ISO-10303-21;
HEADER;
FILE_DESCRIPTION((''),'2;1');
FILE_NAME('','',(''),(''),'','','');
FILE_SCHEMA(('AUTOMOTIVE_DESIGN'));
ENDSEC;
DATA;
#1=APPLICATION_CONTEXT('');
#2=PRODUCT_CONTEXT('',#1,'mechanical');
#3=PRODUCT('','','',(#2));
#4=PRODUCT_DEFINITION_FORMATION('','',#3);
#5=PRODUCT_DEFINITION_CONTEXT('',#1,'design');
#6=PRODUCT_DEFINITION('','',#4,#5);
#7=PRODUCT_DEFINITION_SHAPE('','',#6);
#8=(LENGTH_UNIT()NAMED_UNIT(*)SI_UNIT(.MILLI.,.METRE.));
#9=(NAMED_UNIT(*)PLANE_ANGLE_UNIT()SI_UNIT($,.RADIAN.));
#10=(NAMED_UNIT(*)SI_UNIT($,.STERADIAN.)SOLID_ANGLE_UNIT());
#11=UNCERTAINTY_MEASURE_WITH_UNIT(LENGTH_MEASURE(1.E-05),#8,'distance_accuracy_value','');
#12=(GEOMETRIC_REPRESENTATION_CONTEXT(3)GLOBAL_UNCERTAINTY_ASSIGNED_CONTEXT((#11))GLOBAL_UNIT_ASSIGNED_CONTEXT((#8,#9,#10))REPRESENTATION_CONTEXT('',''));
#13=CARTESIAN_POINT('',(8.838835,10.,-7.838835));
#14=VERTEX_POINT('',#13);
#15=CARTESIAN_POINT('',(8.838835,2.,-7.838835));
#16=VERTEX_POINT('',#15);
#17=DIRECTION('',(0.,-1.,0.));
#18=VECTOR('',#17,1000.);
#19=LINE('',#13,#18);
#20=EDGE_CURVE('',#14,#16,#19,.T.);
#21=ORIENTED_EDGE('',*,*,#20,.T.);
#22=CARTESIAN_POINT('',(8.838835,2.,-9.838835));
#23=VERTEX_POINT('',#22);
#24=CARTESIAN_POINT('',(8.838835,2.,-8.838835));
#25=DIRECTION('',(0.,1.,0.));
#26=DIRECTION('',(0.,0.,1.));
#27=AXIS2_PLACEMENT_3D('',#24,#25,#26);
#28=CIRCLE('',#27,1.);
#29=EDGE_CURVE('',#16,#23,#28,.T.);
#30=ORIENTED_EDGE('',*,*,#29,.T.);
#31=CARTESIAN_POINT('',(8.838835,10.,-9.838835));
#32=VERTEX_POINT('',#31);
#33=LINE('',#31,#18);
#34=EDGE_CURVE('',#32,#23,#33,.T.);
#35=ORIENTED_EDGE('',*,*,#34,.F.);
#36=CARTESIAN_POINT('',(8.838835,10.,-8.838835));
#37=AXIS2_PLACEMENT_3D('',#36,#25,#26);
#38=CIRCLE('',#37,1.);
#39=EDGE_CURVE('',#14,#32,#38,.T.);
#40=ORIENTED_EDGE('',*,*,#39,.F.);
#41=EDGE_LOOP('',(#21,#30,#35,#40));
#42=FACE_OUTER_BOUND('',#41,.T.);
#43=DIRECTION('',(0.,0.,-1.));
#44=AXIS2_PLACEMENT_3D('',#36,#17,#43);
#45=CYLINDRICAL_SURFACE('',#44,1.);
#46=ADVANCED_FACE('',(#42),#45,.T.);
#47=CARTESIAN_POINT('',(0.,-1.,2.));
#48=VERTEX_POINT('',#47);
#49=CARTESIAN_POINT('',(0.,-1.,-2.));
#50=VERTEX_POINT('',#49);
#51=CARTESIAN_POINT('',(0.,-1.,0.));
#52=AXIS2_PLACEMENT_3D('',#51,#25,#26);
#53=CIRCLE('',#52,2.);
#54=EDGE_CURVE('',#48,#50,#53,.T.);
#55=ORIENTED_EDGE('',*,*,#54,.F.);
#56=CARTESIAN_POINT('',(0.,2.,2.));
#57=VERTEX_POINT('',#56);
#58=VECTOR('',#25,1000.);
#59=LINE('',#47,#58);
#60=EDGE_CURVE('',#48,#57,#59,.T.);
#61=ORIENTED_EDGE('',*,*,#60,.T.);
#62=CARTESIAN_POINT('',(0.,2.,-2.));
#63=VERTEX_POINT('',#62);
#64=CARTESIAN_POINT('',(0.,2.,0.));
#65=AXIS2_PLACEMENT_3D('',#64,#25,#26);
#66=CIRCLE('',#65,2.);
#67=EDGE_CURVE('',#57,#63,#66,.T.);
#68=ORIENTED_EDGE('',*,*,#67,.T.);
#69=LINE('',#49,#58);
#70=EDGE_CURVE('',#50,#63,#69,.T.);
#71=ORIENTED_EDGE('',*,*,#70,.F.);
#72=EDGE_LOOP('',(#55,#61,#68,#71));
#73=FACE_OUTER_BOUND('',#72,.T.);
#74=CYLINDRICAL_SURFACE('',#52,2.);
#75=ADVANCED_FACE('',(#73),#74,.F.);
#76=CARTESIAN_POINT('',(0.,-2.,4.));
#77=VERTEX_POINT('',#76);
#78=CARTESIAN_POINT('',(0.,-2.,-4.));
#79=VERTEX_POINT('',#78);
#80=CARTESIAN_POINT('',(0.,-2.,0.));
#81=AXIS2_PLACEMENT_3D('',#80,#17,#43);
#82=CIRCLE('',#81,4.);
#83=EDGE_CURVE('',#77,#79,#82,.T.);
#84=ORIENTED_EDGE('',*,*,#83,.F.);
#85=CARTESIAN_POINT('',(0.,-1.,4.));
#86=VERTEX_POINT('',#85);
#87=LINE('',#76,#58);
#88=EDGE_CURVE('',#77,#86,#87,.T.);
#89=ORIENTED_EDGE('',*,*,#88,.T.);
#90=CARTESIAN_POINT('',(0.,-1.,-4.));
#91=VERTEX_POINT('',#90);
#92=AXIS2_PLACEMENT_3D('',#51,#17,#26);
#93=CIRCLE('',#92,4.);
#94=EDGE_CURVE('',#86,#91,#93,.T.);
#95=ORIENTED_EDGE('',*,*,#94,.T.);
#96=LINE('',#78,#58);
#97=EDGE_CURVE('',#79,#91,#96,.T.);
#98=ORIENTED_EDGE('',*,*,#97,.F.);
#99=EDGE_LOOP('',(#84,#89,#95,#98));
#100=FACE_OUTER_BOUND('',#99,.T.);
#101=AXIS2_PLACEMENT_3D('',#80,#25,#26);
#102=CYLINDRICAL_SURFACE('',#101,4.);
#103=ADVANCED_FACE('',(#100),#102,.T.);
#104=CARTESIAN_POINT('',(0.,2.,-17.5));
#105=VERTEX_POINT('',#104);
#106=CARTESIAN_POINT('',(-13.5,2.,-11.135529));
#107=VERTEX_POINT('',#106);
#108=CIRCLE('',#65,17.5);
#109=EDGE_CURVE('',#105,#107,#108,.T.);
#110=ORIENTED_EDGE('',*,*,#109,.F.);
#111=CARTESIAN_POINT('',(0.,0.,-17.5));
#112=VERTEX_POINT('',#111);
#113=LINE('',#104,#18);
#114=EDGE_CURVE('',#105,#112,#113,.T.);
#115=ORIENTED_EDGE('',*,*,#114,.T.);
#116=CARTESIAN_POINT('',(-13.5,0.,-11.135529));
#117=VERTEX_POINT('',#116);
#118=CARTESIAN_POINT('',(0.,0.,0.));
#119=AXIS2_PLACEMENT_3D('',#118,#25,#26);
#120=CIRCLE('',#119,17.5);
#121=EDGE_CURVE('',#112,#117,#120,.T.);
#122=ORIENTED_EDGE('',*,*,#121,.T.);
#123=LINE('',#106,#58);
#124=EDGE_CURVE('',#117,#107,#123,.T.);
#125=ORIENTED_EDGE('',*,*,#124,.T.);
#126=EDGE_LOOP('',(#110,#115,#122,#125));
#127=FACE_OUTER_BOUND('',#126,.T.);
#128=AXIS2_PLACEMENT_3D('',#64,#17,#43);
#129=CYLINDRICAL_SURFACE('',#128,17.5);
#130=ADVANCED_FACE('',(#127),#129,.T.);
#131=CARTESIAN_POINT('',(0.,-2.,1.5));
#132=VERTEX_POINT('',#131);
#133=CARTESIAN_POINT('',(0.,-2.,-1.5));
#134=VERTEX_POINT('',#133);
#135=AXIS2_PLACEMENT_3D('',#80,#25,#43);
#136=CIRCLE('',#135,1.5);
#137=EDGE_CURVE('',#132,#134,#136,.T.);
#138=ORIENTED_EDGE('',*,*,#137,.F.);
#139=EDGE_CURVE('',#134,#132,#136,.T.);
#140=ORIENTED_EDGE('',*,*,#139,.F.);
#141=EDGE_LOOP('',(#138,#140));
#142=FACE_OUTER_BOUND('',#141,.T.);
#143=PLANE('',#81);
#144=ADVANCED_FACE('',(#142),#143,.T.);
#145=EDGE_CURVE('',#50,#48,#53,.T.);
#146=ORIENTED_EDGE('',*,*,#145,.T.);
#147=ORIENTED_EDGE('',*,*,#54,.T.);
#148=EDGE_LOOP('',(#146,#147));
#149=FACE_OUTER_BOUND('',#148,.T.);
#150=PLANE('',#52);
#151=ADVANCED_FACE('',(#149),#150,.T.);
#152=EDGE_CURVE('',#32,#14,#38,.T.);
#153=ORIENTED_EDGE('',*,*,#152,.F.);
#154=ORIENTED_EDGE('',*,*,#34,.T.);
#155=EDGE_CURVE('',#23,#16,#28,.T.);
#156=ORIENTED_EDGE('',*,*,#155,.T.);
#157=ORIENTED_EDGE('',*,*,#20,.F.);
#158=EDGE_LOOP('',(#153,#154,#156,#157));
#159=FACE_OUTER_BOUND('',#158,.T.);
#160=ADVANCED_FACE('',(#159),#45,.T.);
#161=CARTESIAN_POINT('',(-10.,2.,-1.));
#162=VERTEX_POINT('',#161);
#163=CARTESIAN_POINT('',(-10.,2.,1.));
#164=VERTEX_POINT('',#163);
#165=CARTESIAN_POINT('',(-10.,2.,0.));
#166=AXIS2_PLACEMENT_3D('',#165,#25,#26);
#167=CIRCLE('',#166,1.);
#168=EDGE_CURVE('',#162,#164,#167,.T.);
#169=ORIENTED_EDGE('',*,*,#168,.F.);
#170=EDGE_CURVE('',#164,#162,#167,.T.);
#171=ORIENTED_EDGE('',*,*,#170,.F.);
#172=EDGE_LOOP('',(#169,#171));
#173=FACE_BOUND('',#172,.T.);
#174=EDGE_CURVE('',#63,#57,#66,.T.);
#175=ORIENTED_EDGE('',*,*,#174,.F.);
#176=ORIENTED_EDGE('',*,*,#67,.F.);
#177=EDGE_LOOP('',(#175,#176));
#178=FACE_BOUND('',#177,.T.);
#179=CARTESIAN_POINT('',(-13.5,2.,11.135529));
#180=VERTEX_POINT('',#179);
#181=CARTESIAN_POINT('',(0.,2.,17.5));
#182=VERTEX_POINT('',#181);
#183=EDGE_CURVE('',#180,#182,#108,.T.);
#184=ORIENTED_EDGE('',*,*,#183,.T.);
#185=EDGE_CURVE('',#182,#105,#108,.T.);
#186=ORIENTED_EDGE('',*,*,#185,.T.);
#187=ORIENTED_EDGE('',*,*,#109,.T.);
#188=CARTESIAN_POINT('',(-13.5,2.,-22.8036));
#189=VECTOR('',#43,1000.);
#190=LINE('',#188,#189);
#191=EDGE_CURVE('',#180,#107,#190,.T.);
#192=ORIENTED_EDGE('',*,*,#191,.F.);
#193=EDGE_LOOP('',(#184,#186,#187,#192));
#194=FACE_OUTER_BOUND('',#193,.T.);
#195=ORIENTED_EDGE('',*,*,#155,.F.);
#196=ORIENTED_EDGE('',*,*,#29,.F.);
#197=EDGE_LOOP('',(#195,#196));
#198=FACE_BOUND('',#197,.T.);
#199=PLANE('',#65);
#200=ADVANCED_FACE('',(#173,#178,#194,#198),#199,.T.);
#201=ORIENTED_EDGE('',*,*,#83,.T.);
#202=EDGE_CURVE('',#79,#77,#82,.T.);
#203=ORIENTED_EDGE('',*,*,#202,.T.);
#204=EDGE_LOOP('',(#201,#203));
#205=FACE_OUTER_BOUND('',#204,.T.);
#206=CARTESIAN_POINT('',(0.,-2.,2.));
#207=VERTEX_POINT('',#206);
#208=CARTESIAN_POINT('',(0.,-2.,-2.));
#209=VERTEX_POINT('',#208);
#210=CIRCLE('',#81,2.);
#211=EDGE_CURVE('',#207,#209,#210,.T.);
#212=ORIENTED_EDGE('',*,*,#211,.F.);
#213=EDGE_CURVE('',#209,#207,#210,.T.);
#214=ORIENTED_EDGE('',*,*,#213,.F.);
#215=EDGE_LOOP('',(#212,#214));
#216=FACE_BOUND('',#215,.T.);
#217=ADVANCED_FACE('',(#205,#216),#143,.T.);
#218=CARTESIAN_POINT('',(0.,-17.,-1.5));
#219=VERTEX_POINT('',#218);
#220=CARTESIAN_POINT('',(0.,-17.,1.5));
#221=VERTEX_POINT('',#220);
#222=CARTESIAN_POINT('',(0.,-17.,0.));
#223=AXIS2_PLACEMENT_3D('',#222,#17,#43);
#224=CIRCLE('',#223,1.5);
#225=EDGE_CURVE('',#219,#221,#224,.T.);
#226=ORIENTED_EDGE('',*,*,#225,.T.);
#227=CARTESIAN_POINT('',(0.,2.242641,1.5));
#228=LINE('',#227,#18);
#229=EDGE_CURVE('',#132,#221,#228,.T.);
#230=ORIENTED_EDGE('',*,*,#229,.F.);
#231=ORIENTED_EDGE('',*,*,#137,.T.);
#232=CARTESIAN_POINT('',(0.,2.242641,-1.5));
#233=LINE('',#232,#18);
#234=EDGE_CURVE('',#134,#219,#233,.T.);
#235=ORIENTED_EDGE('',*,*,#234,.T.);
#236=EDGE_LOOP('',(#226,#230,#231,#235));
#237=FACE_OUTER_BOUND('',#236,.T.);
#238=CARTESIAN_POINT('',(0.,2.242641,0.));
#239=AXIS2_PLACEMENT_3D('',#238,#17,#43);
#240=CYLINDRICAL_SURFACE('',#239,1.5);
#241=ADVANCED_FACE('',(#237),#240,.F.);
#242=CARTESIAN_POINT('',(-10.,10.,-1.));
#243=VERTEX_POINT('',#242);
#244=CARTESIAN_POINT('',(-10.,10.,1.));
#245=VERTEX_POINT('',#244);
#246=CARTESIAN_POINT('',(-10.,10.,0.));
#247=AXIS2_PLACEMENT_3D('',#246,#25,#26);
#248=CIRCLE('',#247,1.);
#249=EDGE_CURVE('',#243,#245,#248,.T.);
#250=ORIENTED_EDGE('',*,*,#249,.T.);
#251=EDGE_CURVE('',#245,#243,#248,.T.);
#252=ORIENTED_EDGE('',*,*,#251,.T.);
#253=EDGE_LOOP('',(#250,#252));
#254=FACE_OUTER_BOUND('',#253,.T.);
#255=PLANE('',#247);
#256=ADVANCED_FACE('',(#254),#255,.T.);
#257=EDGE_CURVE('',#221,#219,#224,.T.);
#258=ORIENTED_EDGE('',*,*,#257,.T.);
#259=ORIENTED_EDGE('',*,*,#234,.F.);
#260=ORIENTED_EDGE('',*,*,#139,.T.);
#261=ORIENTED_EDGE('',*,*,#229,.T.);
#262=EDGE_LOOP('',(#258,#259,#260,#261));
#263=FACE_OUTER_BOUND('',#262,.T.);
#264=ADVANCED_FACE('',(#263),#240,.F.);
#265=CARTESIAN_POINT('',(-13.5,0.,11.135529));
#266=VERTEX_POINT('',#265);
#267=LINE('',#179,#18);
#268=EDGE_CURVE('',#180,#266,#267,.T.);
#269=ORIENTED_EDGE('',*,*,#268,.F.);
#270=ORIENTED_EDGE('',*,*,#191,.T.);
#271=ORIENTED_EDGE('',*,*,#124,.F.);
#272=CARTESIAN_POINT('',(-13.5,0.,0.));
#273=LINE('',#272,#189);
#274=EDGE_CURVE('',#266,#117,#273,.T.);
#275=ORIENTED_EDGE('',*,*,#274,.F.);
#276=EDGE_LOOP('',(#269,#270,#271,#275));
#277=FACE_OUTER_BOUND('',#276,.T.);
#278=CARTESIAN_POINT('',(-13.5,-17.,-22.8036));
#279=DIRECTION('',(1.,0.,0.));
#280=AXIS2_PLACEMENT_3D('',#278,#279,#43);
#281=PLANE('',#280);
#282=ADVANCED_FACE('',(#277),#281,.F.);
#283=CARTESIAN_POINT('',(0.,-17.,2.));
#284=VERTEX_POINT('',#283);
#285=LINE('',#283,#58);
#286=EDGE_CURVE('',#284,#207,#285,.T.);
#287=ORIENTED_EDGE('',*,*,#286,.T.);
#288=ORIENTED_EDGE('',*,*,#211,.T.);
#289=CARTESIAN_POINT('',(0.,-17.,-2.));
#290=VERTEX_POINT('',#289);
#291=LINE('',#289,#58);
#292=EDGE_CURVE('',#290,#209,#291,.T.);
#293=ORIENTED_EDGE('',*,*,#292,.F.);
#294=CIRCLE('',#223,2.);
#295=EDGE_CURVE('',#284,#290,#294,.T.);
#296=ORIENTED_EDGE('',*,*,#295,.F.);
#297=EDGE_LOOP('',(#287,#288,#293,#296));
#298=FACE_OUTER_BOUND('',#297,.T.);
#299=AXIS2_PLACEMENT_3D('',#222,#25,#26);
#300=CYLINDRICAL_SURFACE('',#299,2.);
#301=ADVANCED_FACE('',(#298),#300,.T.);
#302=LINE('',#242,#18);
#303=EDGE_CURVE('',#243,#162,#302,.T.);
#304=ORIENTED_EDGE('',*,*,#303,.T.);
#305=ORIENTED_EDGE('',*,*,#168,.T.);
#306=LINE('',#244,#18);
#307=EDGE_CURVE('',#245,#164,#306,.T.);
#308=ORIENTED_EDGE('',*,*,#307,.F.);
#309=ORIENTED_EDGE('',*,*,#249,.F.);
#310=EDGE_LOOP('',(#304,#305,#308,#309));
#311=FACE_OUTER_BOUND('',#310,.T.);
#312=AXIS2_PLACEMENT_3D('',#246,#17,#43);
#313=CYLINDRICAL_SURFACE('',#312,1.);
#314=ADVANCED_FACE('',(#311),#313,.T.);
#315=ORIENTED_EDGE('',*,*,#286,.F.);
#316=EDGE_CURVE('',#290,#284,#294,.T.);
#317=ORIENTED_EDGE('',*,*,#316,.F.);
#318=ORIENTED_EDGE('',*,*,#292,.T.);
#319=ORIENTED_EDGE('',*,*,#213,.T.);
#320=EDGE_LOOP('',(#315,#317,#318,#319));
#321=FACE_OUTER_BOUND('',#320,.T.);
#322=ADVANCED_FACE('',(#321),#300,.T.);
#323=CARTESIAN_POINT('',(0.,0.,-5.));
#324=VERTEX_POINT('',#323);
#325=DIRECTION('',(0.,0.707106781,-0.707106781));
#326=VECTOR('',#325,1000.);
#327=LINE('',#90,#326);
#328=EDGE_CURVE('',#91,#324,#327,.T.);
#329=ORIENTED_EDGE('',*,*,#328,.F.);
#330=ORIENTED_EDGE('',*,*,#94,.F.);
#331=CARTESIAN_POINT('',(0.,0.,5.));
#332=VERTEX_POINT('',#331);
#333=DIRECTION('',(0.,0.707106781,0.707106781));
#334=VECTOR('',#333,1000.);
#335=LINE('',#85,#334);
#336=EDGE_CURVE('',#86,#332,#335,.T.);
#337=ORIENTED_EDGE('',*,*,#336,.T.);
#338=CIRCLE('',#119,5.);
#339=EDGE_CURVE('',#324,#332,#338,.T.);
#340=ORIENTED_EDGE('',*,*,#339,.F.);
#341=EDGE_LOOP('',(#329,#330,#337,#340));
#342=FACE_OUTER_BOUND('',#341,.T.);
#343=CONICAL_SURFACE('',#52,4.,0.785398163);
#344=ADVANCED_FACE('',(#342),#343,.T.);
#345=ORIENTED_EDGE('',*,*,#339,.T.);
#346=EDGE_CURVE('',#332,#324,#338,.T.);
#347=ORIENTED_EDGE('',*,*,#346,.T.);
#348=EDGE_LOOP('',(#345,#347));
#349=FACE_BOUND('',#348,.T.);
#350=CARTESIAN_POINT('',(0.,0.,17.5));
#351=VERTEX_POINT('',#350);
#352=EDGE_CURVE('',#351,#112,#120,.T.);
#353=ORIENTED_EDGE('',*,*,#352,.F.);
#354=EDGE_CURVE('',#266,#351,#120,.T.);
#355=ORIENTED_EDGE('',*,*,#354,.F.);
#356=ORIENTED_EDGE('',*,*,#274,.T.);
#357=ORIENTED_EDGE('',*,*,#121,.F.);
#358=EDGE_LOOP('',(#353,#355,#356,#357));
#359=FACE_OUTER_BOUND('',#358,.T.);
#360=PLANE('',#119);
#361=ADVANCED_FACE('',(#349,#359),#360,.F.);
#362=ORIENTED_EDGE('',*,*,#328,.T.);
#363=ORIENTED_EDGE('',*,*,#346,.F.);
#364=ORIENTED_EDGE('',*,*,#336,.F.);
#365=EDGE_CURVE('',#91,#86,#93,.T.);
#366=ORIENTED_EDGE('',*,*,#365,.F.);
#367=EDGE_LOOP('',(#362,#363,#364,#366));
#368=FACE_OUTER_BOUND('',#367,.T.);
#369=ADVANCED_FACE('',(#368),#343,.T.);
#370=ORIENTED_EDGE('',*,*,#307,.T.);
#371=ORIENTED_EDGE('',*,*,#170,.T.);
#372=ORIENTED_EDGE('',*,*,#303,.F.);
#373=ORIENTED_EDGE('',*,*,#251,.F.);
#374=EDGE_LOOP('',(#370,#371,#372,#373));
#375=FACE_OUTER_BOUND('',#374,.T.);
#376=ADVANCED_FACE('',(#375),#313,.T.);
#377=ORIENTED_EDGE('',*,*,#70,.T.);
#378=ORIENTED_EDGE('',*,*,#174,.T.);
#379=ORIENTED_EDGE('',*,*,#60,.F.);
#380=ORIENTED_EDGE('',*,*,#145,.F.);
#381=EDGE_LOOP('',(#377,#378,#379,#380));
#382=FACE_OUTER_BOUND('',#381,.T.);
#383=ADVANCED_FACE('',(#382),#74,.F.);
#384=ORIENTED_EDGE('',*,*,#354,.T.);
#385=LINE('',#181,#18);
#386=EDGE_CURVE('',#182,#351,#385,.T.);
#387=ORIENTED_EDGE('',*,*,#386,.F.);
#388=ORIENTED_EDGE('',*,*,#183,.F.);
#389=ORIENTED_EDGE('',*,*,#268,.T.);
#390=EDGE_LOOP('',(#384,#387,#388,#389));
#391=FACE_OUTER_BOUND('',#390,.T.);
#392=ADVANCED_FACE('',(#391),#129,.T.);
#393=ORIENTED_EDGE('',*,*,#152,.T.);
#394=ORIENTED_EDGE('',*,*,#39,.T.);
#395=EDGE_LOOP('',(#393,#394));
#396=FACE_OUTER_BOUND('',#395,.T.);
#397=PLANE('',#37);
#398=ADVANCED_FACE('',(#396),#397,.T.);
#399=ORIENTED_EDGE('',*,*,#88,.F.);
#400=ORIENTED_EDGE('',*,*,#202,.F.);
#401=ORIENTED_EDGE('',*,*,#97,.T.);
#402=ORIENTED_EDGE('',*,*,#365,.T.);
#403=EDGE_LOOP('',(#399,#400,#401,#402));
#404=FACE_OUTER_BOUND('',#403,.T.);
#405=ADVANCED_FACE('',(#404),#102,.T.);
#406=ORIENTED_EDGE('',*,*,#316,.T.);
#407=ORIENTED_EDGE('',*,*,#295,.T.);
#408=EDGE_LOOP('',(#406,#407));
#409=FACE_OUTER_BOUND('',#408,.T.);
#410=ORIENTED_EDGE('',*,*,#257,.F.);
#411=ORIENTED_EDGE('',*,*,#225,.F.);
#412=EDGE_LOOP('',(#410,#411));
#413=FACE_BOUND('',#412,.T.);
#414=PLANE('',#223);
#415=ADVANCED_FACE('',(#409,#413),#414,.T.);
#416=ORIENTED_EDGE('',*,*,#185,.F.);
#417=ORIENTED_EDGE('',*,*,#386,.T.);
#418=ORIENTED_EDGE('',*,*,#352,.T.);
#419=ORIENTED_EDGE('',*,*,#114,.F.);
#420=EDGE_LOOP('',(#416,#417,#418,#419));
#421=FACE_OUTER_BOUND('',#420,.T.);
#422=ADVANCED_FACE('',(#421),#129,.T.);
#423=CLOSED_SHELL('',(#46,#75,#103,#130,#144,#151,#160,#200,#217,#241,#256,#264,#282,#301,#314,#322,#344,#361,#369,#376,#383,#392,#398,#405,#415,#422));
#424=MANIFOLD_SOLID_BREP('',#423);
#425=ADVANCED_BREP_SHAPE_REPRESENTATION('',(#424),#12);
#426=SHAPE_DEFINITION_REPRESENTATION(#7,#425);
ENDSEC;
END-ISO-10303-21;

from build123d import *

# Parameters (mm, degrees)
SKETCH1_R           = 17.5
BOSS_EXTRUDE1_DEPTH = 2
SKETCH3_R           = 4
BOSS_EXTRUDE2_DEPTH = 2
CHAMFER1_SIZE       = 1
SKETCH4_R           = 2
BOSS_EXTRUDE3_DEPTH = 15
SKETCH5_R           = 1.5
CUT_EXTRUDE1_DEPTH  = 15
SKETCH6_R           = 1
BOSS_EXTRUDE4_DEPTH = 8
SKETCH7_W           = 4
SKETCH7_H           = 45.60719986
CUT_EXTRUDE2_DEPTH  = 32.200961524
SKETCH8_R           = 2
CUT_EXTRUDE3_DEPTH  = 3


with BuildPart() as part:
    # Sketch1 → Boss-Extrude1 (new body)
    with BuildSketch(Plane(origin=(0, 0, 0), x_dir=(1, 0, 0), z_dir=(0, 1, 0))):
        with Locations(Location((0, 0, 0), (0, 0, 270))):
            Circle(SKETCH1_R)
    extrude(amount=BOSS_EXTRUDE1_DEPTH)

    # Sketch3 → Boss-Extrude2 (add)
    with BuildSketch(Plane.XZ):
        with Locations(Location((0, 0, 0), (0, 0, 270))):
            Circle(SKETCH3_R)
    extrude(amount=BOSS_EXTRUDE2_DEPTH)

    # Chamfer1
    chamfer1_edges = [part.edges().sort_by_distance(p)[0] for p in [
        (0, 0, 4),
    ]]
    chamfer(chamfer1_edges, length=CHAMFER1_SIZE)

    # Sketch4 → Boss-Extrude3 (add)
    with BuildSketch(Plane.XZ.offset(2)):
        with Locations(Location((0, 0, 0), (0, 0, 270))):
            Circle(SKETCH4_R)
    extrude(amount=BOSS_EXTRUDE3_DEPTH)

    # Sketch5 → Cut-Extrude1 (cut)
    with BuildSketch(Plane.XZ.offset(17)):
        with Locations(Location((0, 0, 0), (0, 0, 270))):
            Circle(SKETCH5_R)
    extrude(amount=-CUT_EXTRUDE1_DEPTH, mode=Mode.SUBTRACT)

    # Sketch6 → Boss-Extrude4 (add)
    with BuildSketch(Plane(origin=(0, 2, 0), x_dir=(1, 0, 0), z_dir=(0, 1, 0))):
        with Locations(Location((-10, 0, 0), (0, 0, 270))):
            Circle(SKETCH6_R)
        with Locations(Location((8.838834765, 8.838834765, 0), (0, 0, 270))):
            Circle(SKETCH6_R)
    extrude(amount=BOSS_EXTRUDE4_DEPTH)

    # Sketch7 → Cut-Extrude2 (cut, through all)
    with BuildSketch(Plane(origin=(0, 2, 0), x_dir=(1, 0, 0), z_dir=(0, 1, 0))):
        with Locations((-15.5, 0)):
            Rectangle(SKETCH7_W, SKETCH7_H)
    extrude(amount=-CUT_EXTRUDE2_DEPTH, mode=Mode.SUBTRACT)

    # Sketch8 → Cut-Extrude3 (cut)
    with BuildSketch(Plane(origin=(0, 2, 0), x_dir=(1, 0, 0), z_dir=(0, 1, 0))):
        with Locations(Location((0, 0, 0), (0, 0, 90))):
            Circle(SKETCH8_R)
    extrude(amount=-CUT_EXTRUDE3_DEPTH, mode=Mode.SUBTRACT)


solid = part.part
